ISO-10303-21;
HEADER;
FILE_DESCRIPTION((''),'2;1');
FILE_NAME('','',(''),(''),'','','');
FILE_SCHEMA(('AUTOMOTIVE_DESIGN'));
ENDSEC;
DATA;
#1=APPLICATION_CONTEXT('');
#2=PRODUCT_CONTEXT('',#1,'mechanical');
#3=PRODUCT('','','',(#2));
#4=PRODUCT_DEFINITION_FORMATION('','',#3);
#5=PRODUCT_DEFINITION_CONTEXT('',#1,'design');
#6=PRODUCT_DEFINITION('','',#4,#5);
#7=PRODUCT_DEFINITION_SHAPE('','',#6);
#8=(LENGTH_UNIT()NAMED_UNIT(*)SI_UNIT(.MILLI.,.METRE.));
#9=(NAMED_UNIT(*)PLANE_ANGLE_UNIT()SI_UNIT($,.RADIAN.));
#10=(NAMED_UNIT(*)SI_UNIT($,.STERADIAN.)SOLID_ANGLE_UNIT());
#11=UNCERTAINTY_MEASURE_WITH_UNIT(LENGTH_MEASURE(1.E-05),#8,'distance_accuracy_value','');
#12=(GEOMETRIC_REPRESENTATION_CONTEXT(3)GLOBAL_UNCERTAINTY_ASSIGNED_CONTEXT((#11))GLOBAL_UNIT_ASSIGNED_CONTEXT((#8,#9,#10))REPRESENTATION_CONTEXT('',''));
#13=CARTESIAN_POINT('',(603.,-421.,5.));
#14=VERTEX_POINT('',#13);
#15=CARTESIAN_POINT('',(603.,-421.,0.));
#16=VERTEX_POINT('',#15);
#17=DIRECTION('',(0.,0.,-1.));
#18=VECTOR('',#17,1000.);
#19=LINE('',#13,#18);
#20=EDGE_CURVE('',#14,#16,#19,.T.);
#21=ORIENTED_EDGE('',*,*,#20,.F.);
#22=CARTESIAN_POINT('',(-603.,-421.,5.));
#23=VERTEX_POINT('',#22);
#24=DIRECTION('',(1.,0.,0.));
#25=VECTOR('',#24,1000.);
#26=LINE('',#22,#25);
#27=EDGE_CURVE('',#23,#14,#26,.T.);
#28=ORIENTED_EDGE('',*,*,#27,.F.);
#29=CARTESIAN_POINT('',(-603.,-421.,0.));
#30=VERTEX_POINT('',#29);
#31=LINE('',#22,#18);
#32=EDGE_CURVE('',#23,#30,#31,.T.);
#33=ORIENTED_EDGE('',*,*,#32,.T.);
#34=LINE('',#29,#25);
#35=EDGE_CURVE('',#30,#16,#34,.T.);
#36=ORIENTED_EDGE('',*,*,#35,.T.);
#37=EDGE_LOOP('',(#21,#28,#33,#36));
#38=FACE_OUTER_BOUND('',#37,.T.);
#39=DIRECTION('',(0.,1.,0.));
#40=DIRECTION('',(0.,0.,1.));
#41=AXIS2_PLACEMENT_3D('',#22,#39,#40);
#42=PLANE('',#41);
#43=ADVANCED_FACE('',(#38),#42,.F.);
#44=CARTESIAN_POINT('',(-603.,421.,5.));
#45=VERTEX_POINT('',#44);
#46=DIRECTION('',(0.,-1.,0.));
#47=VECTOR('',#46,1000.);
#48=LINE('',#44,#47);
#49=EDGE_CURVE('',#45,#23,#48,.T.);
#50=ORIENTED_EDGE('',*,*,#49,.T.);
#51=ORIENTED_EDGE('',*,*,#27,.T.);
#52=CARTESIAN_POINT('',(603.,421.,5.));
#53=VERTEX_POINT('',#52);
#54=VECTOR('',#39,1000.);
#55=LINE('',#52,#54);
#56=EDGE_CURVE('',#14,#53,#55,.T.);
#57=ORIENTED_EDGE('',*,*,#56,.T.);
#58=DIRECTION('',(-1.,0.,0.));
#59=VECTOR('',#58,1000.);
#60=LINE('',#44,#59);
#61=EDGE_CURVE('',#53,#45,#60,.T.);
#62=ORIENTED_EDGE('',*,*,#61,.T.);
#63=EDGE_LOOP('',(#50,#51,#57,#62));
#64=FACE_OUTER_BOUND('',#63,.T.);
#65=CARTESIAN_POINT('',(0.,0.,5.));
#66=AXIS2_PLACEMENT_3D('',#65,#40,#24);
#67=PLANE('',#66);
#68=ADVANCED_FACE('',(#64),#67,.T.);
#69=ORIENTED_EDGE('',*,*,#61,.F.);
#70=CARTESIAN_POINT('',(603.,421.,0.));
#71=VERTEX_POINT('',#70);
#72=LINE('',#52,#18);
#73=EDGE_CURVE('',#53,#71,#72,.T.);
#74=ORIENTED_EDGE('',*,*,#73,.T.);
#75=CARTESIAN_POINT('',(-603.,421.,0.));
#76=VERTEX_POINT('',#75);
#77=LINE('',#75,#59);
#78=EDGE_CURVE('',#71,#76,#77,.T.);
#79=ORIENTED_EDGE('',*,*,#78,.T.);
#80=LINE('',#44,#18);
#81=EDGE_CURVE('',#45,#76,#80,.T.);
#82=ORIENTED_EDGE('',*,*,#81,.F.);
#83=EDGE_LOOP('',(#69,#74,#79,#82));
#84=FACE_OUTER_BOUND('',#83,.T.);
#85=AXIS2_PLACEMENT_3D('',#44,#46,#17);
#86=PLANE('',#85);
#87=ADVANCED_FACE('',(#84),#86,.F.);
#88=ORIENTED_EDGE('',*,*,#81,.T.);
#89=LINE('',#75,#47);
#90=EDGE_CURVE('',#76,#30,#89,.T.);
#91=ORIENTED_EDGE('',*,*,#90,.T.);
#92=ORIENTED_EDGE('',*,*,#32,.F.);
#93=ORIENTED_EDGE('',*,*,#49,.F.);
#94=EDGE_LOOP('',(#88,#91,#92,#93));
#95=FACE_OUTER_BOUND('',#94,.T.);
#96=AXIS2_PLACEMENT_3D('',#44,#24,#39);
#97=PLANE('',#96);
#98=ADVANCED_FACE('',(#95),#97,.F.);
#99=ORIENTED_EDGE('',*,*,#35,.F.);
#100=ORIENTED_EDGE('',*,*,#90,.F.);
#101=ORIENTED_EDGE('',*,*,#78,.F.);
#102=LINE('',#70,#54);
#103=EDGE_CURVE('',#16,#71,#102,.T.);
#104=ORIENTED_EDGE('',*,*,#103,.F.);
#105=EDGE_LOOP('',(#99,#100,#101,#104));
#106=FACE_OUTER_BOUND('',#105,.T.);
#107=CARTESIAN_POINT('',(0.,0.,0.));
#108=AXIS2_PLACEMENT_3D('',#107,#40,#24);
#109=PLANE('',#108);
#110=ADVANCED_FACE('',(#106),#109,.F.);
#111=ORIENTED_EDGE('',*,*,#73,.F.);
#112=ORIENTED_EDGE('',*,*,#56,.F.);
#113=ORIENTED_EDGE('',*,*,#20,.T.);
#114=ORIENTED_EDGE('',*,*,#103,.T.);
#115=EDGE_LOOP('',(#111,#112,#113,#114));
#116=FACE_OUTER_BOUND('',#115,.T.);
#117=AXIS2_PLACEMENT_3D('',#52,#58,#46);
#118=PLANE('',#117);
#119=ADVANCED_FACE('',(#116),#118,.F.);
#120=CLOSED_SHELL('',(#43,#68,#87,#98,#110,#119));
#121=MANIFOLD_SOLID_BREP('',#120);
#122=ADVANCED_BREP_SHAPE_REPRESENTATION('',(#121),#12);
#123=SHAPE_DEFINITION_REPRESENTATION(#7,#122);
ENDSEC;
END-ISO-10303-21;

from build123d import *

# Parameters (mm, degrees)
SKETCH_1_W      = 1206
SKETCH_1_H      = 842
EXTRUDE_1_DEPTH = 5


with BuildPart() as part:
    # 草图1 → 凸台-拉伸1 (new body)
    with BuildSketch(Plane.XY):
        Rectangle(SKETCH_1_W, SKETCH_1_H)
    extrude(amount=EXTRUDE_1_DEPTH)


solid = part.part
